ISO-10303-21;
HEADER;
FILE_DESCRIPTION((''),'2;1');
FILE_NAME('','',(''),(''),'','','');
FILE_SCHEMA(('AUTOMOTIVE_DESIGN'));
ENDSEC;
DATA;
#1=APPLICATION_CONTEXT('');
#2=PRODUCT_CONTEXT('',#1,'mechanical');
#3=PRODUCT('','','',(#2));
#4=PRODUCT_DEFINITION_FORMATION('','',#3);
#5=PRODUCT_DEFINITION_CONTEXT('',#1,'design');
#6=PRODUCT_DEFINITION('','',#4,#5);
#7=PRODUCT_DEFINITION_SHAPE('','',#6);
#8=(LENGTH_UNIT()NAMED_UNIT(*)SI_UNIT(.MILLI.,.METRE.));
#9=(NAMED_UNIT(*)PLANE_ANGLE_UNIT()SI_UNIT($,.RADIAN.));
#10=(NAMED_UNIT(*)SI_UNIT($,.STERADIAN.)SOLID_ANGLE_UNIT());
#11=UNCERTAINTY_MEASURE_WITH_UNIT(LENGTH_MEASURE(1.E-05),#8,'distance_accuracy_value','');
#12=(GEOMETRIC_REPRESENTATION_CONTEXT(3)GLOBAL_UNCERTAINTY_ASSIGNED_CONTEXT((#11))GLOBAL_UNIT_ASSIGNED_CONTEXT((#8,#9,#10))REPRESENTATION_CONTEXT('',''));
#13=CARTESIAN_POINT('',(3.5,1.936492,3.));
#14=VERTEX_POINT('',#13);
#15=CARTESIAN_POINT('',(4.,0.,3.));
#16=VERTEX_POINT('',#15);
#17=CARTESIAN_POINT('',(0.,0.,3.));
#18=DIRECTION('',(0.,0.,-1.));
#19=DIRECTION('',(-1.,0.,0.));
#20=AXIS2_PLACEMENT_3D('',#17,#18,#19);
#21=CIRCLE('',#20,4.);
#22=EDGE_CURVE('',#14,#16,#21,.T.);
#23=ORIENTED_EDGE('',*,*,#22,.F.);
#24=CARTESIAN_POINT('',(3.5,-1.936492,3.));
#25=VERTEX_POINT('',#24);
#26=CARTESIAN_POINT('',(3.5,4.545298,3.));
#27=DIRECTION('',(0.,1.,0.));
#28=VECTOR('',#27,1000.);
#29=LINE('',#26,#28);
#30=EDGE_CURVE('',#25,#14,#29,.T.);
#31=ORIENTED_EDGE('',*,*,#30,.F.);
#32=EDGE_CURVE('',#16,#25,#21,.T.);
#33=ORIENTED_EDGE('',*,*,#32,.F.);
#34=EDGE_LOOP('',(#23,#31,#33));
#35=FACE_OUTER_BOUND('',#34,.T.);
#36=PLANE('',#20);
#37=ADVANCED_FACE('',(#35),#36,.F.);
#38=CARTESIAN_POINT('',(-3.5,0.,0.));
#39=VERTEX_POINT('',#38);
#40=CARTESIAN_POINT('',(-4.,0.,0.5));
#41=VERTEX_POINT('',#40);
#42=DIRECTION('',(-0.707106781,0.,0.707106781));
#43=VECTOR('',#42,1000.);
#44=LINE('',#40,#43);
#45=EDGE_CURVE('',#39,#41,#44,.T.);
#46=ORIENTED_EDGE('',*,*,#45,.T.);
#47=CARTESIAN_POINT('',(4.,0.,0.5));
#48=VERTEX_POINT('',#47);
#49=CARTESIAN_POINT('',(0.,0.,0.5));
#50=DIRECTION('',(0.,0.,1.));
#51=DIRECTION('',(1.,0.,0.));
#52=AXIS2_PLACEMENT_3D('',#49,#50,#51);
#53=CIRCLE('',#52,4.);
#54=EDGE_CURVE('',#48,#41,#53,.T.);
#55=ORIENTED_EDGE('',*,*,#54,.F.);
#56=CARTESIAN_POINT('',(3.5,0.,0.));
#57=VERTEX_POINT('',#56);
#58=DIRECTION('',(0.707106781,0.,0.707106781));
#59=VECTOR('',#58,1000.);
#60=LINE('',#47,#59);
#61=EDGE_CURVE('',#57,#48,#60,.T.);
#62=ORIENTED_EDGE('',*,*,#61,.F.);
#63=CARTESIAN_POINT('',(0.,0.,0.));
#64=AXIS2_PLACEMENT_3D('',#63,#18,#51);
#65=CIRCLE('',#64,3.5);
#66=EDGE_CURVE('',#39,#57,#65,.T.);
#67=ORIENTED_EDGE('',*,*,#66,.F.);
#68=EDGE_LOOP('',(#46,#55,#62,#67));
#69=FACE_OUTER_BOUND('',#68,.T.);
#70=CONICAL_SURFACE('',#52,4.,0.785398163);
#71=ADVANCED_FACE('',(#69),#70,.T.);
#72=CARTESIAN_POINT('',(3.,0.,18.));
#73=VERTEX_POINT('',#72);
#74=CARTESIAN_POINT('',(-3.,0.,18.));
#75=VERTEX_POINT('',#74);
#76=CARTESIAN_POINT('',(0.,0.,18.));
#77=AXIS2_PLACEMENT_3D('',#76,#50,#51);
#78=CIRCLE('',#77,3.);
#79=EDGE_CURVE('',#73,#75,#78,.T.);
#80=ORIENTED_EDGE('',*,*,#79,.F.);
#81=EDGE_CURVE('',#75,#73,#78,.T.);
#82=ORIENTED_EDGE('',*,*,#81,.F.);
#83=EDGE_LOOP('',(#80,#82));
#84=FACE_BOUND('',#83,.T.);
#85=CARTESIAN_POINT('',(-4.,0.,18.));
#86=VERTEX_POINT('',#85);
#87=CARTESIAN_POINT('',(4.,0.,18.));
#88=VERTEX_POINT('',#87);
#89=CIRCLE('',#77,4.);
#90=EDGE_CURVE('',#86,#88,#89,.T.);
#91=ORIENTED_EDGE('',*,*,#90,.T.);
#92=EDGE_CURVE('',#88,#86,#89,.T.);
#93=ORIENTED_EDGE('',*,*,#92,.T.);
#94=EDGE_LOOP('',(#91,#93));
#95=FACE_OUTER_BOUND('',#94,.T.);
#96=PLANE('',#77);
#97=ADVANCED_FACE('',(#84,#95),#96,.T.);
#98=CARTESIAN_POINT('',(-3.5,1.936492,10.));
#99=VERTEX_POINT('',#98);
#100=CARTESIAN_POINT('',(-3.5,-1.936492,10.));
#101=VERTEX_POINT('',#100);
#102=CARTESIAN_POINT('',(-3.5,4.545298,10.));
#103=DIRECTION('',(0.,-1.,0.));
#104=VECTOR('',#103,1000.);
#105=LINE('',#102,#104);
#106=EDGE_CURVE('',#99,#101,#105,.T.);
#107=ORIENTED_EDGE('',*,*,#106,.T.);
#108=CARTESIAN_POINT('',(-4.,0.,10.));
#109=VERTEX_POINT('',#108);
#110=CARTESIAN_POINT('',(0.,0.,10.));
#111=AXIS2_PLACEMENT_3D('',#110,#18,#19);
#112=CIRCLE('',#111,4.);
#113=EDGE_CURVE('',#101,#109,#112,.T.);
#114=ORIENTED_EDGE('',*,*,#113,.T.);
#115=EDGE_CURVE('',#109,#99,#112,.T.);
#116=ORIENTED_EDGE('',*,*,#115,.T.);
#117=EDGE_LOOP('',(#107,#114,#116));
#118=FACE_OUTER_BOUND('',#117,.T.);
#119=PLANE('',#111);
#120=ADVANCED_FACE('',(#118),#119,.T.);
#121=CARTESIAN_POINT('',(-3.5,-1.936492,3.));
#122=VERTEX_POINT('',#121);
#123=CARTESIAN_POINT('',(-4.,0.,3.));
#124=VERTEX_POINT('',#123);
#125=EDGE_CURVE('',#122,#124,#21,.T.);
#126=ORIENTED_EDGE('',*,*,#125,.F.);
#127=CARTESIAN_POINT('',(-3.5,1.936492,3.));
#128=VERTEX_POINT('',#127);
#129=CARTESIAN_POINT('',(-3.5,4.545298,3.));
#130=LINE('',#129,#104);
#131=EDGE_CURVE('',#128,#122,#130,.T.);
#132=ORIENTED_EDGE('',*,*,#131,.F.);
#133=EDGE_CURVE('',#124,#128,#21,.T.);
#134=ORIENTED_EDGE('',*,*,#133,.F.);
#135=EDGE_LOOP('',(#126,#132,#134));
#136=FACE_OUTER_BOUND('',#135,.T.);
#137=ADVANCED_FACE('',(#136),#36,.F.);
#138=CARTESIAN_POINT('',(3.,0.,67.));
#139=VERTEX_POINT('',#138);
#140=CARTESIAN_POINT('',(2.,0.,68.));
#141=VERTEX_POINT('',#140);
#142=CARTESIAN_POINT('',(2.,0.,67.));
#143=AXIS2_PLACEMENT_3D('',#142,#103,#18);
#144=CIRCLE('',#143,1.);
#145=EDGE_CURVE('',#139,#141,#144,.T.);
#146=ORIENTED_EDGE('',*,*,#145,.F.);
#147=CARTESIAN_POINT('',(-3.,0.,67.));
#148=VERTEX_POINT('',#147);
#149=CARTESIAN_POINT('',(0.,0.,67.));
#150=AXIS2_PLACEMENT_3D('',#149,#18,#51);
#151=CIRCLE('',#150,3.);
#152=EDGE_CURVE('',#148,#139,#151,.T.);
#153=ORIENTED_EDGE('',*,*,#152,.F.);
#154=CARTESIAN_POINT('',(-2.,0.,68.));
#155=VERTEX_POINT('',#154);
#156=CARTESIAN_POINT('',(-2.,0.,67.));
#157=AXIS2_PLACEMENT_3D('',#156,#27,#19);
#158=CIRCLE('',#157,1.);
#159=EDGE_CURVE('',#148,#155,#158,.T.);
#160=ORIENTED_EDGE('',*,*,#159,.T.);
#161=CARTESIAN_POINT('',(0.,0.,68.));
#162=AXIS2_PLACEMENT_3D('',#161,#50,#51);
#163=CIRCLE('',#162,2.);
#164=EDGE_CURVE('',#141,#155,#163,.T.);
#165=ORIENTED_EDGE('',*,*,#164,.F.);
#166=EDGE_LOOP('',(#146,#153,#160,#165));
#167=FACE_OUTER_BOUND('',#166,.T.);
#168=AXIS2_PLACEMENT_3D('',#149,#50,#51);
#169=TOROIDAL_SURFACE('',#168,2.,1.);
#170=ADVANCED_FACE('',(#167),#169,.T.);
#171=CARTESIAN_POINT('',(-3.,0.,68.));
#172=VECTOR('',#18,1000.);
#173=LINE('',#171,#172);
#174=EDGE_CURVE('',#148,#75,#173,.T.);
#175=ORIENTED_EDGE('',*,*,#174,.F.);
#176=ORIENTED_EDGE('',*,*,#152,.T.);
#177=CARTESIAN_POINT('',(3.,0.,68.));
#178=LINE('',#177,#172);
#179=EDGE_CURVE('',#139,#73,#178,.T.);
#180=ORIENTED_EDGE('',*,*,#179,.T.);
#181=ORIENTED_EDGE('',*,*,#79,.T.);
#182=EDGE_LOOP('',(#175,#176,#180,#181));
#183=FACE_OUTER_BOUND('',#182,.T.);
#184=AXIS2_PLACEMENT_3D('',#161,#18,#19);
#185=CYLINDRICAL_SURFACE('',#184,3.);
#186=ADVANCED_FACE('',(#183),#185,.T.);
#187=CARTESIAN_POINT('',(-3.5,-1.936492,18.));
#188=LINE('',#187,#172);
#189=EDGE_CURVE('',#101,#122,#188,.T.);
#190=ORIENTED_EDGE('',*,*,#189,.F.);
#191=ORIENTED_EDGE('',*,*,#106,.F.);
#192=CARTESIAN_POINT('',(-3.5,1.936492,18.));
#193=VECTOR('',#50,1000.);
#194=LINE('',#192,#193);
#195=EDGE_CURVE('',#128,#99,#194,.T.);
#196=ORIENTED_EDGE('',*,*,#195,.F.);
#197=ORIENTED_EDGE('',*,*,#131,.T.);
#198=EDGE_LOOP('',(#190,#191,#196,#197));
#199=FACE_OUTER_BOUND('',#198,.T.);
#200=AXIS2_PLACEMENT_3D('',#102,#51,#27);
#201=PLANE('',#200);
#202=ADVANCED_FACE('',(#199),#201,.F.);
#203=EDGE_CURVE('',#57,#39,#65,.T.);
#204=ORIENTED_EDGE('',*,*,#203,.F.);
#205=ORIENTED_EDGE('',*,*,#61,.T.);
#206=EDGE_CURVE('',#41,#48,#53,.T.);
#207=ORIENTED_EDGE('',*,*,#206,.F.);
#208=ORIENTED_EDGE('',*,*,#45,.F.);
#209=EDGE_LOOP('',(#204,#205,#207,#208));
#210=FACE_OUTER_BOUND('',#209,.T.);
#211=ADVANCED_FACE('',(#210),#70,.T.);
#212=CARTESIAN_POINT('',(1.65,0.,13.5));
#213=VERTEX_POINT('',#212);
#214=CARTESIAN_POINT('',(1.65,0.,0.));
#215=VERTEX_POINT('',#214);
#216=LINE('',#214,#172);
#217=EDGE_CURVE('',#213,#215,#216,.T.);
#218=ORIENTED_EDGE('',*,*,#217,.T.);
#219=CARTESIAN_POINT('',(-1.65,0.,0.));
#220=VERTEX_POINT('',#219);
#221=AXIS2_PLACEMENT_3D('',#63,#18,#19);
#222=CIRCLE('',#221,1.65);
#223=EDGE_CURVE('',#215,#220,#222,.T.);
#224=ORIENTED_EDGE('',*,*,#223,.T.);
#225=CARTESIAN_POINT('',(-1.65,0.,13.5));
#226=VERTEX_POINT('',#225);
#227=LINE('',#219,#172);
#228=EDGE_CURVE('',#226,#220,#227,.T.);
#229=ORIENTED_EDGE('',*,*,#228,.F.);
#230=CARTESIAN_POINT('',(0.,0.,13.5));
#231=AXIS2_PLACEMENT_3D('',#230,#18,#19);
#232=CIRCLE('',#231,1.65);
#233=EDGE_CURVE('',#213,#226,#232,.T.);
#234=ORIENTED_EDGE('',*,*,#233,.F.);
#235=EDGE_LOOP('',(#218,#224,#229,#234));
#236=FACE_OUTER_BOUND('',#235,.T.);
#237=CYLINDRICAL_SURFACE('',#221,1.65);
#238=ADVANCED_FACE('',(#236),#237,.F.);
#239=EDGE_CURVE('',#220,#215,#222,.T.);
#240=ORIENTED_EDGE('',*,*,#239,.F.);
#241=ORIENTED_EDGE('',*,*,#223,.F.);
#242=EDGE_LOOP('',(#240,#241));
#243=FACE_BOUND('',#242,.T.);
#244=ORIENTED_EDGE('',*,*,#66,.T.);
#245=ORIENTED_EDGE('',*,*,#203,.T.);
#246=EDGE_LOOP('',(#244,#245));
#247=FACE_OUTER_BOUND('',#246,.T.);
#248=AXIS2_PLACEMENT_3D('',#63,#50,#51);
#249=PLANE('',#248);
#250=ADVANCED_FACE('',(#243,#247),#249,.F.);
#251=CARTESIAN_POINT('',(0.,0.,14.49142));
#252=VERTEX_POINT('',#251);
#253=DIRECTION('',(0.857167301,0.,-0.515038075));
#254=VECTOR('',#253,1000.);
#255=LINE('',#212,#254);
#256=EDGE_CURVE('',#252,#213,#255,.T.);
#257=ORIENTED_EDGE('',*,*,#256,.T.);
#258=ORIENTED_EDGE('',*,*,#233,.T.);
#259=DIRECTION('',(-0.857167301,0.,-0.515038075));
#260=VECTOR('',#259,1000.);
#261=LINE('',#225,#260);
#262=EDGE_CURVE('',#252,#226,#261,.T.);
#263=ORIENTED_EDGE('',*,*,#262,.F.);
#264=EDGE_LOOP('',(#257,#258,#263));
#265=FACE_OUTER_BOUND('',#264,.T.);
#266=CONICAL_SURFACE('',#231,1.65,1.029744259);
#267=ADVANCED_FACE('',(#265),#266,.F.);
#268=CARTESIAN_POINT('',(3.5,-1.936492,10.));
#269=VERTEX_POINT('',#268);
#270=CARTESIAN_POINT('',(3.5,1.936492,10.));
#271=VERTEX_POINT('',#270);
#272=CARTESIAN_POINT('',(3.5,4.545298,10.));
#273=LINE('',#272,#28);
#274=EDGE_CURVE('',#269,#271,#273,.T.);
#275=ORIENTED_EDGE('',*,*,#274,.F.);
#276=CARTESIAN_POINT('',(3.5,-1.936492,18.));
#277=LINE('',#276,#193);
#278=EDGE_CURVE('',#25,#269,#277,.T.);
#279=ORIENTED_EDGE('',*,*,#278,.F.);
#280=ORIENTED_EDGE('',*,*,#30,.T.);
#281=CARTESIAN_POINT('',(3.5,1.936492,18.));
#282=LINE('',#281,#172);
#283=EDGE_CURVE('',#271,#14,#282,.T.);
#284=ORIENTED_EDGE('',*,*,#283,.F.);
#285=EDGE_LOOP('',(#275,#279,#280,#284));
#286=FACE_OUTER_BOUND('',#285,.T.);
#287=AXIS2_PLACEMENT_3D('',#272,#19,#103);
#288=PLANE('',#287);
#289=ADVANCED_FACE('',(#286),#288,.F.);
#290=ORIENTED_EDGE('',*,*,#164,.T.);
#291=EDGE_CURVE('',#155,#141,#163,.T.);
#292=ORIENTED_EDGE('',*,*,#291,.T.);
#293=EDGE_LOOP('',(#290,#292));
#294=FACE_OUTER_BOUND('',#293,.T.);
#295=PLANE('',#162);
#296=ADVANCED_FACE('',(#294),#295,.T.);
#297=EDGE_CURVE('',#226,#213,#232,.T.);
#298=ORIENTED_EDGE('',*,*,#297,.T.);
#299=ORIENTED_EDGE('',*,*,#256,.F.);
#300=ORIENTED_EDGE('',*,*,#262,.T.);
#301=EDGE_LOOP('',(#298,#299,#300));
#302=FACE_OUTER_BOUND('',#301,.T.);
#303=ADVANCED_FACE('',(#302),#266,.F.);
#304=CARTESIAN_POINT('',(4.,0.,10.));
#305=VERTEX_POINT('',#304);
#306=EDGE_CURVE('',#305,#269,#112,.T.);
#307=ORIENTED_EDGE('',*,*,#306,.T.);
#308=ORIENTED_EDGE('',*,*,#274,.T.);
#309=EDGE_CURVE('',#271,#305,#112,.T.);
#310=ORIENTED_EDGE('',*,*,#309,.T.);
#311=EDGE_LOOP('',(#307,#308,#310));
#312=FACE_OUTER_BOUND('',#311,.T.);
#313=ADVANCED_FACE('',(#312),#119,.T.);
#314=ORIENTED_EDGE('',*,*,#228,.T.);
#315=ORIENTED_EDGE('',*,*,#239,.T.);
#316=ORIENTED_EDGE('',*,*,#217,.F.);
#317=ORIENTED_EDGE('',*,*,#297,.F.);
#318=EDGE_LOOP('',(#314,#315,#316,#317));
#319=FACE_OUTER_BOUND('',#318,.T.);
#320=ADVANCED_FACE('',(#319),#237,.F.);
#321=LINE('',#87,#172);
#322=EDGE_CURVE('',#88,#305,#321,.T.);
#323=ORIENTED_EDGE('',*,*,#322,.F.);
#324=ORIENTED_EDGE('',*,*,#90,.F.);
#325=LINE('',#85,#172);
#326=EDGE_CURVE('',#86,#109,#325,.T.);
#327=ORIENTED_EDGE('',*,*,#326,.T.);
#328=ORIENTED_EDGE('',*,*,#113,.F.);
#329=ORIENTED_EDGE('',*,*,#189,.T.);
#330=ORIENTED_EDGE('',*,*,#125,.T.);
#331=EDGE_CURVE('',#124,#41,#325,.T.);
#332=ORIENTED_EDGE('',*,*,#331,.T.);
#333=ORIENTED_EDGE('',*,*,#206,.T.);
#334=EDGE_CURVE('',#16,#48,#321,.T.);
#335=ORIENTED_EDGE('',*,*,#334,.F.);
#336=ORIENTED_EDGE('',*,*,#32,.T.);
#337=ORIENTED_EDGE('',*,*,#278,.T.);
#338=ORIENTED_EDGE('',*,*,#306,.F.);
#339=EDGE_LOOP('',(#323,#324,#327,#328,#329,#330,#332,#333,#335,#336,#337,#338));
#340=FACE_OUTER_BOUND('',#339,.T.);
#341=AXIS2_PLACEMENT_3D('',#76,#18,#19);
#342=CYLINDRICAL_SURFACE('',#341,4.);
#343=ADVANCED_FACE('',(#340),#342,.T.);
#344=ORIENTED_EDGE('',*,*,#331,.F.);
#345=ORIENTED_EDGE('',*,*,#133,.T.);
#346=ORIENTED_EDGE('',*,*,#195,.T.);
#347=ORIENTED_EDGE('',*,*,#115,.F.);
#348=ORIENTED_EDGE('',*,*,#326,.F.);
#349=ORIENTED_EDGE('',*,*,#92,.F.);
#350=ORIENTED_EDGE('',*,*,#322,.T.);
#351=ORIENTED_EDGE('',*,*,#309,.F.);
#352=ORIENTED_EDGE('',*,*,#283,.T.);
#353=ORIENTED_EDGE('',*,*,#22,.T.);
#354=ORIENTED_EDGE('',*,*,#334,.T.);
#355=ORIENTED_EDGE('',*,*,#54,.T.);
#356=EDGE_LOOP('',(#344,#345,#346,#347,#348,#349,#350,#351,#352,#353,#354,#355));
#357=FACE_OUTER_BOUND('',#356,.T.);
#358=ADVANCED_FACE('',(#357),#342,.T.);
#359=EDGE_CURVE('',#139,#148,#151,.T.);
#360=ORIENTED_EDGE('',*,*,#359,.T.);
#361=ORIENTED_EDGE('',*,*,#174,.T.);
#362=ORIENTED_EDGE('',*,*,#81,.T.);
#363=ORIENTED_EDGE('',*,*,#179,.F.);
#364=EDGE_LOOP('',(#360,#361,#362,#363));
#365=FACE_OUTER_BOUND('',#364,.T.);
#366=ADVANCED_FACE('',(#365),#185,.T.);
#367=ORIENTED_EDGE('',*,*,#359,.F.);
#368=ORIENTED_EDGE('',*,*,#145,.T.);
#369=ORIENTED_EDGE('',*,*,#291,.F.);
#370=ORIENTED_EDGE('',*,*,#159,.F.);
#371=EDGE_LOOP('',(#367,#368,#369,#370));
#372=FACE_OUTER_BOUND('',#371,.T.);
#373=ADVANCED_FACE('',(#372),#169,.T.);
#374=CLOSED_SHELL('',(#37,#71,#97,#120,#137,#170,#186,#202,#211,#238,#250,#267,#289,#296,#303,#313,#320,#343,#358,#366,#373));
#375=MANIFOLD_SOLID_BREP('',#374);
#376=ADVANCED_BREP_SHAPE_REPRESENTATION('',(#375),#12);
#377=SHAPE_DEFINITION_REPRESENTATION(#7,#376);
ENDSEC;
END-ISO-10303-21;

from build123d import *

# Parameters (mm, degrees)
SKETCH_1_R             = 4
EXTRUDE_1_DEPTH        = 18
SKETCH_2_R             = 3
EXTRUDE_2_DEPTH        = 50
FILLET_1_R             = 1
CHAMFER_1_SIZE         = 0.5
HOLE_WIZARD_M4_1_D     = 3.3
HOLE_WIZARD_M4_1_DEPTH = 13.5
HOLE_WIZARD_M4_1_TIP   = 0.991420021
SKETCH_5_W             = 2.600851977
SKETCH_5_H             = 9.759387418
SKETCH_5_W_2           = 4.309983276
SKETCH_5_H_2           = 9.585997286
CUT_EXTRUDE_1_DEPTH    = 7


with BuildPart() as part:
    # 草图1 → 凸台-拉伸1 (new body)
    with BuildSketch(Plane.XY):
        Circle(SKETCH_1_R)
    extrude(amount=EXTRUDE_1_DEPTH)

    # 草图2 → 凸台-拉伸2 (add)
    with BuildSketch(Plane.XY.offset(18)):
        Circle(SKETCH_2_R)
    extrude(amount=EXTRUDE_2_DEPTH)

    # 圆角1
    fillet_1_edges = [part.edges().sort_by_distance(p)[0] for p in [
        (-3, 0, 68),
    ]]
    fillet(fillet_1_edges, radius=FILLET_1_R)

    # 倒角1
    chamfer_1_edges = [part.edges().sort_by_distance(p)[0] for p in [
        (-4, 0, 0),
    ]]
    chamfer(chamfer_1_edges, length=CHAMFER_1_SIZE)

    # M4 螺纹孔1
    with Locations(Plane(origin=(0, 0, 0), x_dir=(-1, 0, 0), z_dir=(0, 0, -1))):
        with Locations((0, 0)):
            Hole(HOLE_WIZARD_M4_1_D / 2, depth=HOLE_WIZARD_M4_1_DEPTH)
            with Locations((0, 0, -(HOLE_WIZARD_M4_1_DEPTH + HOLE_WIZARD_M4_1_TIP / 2))):  # 118° drill point
                Cone(0, HOLE_WIZARD_M4_1_D / 2, HOLE_WIZARD_M4_1_TIP, mode=Mode.SUBTRACT)

    # 草图5 → 切除-拉伸1 (cut)
    with BuildSketch(Plane(origin=(0, 0, 3), x_dir=(-1, 0, 0), z_dir=(0, 0, -1))):
        with Locations((-4.800425989, -0.334395254)):
            Rectangle(SKETCH_5_W, SKETCH_5_H)
        with Locations((5.654991638, -0.247700188)):
            Rectangle(SKETCH_5_W_2, SKETCH_5_H_2)
    extrude(amount=-CUT_EXTRUDE_1_DEPTH, mode=Mode.SUBTRACT)


solid = part.part
